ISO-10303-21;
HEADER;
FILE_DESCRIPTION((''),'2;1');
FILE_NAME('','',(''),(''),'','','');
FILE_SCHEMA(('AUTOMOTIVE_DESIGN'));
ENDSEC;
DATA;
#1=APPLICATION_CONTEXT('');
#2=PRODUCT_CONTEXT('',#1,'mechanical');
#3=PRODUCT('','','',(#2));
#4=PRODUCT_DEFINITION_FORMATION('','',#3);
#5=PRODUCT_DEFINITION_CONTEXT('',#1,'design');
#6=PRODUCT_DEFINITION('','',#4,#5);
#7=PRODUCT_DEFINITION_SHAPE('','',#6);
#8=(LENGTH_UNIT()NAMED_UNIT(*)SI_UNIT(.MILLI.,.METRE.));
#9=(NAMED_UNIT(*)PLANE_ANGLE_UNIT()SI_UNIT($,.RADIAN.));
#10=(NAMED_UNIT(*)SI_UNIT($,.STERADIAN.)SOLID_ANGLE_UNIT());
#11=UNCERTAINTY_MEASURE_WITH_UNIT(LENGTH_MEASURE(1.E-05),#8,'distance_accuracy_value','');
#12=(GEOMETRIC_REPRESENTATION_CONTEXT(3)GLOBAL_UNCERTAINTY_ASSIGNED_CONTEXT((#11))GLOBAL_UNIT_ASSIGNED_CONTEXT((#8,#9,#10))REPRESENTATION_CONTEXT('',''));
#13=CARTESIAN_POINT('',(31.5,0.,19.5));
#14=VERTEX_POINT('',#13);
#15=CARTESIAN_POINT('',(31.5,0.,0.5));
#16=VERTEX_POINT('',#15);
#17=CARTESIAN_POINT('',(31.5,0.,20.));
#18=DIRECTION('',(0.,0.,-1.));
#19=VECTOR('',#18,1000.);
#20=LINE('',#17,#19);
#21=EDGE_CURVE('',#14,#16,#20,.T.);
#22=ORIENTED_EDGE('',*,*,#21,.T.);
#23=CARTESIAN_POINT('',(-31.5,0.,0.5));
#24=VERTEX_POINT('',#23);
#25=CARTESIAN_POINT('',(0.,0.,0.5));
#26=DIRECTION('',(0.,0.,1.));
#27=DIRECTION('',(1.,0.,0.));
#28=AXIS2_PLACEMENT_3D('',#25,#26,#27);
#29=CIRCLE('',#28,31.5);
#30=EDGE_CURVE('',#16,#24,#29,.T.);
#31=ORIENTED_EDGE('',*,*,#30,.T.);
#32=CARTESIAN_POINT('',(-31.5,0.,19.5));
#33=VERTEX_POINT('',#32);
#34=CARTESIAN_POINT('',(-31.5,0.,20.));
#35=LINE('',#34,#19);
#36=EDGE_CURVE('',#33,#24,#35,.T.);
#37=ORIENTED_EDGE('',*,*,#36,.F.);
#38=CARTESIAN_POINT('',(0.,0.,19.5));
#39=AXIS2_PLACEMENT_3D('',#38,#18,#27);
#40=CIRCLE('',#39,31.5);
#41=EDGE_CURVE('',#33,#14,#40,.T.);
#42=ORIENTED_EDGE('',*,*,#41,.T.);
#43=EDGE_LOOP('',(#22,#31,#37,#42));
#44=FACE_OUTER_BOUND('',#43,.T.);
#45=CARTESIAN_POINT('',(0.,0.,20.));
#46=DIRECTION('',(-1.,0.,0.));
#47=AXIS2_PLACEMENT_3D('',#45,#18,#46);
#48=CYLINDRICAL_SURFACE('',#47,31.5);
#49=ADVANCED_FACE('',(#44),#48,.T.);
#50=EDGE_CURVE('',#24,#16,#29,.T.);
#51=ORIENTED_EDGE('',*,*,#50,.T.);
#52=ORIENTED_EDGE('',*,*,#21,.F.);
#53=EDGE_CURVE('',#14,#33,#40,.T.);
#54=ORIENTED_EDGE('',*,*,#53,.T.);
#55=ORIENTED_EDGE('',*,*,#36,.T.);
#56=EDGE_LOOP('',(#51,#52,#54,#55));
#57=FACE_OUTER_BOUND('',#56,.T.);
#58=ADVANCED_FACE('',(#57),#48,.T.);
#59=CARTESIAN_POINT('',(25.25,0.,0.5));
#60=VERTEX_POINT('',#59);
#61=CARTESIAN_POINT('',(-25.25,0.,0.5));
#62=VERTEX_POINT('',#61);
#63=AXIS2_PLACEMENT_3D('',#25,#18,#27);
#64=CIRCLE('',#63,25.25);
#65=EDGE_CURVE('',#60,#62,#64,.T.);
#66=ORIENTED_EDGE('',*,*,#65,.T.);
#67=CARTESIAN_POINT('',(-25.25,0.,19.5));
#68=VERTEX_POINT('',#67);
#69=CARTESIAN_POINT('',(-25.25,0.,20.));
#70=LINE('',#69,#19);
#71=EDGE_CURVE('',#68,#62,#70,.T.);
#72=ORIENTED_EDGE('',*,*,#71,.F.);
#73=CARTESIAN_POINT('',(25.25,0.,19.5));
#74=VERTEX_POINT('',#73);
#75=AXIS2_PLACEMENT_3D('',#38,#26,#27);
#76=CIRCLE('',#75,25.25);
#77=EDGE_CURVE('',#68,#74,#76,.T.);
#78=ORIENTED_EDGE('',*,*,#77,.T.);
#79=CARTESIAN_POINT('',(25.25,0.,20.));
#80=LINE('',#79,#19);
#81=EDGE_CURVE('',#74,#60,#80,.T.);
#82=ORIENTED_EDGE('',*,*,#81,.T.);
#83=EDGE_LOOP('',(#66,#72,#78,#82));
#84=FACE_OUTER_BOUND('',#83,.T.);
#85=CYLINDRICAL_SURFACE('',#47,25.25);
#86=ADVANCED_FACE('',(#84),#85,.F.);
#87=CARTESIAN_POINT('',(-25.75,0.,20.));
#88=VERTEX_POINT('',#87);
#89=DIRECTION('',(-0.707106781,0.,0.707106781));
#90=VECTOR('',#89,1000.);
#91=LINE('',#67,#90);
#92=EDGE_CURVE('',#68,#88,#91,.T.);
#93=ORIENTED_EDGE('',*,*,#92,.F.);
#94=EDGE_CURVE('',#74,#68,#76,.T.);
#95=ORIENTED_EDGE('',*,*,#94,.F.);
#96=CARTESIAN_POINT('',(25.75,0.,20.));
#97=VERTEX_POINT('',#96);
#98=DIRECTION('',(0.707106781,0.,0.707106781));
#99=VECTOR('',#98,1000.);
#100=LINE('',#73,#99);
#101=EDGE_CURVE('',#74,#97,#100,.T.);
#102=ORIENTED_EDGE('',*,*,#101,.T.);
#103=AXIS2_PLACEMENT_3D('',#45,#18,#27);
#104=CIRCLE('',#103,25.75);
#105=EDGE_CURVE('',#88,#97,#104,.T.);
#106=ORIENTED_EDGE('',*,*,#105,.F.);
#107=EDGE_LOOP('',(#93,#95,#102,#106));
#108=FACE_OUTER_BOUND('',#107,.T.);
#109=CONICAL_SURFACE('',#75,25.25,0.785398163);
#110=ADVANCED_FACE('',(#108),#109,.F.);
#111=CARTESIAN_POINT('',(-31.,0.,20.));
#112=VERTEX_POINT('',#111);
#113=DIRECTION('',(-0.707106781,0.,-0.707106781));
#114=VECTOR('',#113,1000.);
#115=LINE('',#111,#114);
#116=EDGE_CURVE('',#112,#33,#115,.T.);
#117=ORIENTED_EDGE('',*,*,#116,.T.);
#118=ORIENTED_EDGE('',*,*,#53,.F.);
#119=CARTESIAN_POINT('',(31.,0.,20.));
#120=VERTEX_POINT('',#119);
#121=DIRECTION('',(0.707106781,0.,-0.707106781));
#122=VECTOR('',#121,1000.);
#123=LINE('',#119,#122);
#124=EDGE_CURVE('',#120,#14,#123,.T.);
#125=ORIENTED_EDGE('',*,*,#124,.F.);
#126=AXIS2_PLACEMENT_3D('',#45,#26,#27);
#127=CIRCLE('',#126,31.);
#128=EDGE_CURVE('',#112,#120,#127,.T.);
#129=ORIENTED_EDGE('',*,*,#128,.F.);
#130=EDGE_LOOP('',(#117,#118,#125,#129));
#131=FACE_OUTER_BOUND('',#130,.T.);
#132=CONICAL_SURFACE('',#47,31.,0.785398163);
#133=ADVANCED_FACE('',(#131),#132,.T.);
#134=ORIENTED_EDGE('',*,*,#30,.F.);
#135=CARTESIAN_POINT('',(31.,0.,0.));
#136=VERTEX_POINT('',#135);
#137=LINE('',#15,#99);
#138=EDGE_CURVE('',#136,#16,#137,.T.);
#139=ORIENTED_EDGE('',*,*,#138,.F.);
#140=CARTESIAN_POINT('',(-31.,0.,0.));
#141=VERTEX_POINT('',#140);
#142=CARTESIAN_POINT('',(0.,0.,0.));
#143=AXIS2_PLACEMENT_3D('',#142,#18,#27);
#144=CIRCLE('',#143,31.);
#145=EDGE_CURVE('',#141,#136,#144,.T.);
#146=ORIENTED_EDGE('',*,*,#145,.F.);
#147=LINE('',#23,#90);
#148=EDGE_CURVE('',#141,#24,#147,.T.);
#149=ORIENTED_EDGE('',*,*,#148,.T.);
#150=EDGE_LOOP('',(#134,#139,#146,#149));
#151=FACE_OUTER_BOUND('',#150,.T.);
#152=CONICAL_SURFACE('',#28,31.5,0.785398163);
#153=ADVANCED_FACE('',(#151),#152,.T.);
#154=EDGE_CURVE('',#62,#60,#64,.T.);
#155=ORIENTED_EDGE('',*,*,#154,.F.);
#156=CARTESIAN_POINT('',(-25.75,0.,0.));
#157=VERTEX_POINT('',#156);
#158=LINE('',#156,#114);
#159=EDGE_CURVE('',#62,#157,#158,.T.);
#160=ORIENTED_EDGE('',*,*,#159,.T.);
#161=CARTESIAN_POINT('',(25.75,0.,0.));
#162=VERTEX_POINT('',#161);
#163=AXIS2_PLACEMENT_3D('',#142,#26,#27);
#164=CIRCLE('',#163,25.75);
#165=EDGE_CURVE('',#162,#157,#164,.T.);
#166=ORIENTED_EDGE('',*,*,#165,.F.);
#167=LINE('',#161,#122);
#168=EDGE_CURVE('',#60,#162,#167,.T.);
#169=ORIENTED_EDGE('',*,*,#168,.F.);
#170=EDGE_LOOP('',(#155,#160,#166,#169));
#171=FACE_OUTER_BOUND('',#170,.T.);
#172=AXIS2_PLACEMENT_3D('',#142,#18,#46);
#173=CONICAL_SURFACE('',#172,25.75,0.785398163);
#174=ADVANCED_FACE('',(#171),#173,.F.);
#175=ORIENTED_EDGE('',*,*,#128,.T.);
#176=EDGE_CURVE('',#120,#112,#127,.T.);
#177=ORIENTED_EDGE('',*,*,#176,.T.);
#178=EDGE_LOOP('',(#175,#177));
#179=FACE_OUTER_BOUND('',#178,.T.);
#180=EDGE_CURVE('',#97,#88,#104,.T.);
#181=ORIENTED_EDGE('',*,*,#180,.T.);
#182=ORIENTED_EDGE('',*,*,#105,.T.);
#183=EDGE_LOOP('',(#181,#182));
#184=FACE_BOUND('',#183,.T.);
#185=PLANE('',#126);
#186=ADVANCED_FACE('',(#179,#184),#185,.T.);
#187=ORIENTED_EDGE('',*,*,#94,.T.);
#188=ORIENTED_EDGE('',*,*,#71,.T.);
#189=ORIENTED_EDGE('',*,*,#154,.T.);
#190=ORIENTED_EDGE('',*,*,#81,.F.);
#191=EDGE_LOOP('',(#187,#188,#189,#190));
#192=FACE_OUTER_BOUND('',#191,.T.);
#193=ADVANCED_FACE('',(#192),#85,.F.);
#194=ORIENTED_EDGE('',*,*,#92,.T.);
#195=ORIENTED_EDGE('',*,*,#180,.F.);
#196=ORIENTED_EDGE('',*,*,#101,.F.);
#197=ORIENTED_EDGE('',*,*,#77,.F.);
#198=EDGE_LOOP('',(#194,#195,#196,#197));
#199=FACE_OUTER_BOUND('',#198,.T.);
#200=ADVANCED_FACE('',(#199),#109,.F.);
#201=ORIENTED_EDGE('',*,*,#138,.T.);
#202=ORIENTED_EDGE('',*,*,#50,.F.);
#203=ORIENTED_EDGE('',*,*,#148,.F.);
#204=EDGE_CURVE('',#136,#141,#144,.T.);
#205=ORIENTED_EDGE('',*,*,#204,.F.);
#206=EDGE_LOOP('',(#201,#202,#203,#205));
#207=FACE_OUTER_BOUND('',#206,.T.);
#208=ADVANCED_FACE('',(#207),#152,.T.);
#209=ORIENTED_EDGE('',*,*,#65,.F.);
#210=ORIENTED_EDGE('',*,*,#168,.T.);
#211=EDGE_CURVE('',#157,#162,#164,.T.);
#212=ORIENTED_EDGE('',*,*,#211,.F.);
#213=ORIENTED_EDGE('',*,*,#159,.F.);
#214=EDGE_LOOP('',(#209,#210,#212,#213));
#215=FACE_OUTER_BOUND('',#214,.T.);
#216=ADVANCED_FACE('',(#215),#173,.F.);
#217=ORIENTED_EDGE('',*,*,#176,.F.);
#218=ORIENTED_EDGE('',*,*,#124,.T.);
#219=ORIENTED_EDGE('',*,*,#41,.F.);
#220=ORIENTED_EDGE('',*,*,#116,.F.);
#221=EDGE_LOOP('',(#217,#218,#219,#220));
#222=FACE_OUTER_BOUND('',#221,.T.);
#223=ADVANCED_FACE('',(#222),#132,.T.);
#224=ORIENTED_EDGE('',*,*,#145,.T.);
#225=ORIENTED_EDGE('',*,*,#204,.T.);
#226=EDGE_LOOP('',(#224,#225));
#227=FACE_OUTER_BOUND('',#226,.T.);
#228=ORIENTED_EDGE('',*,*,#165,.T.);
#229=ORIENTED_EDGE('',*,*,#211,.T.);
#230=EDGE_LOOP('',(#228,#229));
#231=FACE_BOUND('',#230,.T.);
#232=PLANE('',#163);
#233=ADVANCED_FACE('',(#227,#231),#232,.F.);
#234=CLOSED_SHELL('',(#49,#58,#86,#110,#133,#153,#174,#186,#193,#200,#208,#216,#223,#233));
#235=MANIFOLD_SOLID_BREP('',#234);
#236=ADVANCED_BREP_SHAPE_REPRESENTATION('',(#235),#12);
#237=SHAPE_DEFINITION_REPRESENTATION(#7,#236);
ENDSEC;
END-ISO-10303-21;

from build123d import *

# Parameters (mm, degrees)
SKETCH_1_R      = 31.5
SKETCH_1_R_2    = 25.25
EXTRUDE_1_DEPTH = 20
CHAMFER_1_SIZE  = 0.5


with BuildPart() as part:
    # 草图1 → 凸台-拉伸1 (new body)
    with BuildSketch(Plane.XY):
        Circle(SKETCH_1_R)
        Circle(SKETCH_1_R_2, mode=Mode.SUBTRACT)
    extrude(amount=EXTRUDE_1_DEPTH)

    # 倒角1
    chamfer_1_edges = [part.edges().sort_by_distance(p)[0] for p in [
        (-31.5, 0, 0),
        (-31.5, 0, 20),
        (-25.25, 0, 0),
        (-25.25, 0, 20),
    ]]
    chamfer(chamfer_1_edges, length=CHAMFER_1_SIZE)


solid = part.part
